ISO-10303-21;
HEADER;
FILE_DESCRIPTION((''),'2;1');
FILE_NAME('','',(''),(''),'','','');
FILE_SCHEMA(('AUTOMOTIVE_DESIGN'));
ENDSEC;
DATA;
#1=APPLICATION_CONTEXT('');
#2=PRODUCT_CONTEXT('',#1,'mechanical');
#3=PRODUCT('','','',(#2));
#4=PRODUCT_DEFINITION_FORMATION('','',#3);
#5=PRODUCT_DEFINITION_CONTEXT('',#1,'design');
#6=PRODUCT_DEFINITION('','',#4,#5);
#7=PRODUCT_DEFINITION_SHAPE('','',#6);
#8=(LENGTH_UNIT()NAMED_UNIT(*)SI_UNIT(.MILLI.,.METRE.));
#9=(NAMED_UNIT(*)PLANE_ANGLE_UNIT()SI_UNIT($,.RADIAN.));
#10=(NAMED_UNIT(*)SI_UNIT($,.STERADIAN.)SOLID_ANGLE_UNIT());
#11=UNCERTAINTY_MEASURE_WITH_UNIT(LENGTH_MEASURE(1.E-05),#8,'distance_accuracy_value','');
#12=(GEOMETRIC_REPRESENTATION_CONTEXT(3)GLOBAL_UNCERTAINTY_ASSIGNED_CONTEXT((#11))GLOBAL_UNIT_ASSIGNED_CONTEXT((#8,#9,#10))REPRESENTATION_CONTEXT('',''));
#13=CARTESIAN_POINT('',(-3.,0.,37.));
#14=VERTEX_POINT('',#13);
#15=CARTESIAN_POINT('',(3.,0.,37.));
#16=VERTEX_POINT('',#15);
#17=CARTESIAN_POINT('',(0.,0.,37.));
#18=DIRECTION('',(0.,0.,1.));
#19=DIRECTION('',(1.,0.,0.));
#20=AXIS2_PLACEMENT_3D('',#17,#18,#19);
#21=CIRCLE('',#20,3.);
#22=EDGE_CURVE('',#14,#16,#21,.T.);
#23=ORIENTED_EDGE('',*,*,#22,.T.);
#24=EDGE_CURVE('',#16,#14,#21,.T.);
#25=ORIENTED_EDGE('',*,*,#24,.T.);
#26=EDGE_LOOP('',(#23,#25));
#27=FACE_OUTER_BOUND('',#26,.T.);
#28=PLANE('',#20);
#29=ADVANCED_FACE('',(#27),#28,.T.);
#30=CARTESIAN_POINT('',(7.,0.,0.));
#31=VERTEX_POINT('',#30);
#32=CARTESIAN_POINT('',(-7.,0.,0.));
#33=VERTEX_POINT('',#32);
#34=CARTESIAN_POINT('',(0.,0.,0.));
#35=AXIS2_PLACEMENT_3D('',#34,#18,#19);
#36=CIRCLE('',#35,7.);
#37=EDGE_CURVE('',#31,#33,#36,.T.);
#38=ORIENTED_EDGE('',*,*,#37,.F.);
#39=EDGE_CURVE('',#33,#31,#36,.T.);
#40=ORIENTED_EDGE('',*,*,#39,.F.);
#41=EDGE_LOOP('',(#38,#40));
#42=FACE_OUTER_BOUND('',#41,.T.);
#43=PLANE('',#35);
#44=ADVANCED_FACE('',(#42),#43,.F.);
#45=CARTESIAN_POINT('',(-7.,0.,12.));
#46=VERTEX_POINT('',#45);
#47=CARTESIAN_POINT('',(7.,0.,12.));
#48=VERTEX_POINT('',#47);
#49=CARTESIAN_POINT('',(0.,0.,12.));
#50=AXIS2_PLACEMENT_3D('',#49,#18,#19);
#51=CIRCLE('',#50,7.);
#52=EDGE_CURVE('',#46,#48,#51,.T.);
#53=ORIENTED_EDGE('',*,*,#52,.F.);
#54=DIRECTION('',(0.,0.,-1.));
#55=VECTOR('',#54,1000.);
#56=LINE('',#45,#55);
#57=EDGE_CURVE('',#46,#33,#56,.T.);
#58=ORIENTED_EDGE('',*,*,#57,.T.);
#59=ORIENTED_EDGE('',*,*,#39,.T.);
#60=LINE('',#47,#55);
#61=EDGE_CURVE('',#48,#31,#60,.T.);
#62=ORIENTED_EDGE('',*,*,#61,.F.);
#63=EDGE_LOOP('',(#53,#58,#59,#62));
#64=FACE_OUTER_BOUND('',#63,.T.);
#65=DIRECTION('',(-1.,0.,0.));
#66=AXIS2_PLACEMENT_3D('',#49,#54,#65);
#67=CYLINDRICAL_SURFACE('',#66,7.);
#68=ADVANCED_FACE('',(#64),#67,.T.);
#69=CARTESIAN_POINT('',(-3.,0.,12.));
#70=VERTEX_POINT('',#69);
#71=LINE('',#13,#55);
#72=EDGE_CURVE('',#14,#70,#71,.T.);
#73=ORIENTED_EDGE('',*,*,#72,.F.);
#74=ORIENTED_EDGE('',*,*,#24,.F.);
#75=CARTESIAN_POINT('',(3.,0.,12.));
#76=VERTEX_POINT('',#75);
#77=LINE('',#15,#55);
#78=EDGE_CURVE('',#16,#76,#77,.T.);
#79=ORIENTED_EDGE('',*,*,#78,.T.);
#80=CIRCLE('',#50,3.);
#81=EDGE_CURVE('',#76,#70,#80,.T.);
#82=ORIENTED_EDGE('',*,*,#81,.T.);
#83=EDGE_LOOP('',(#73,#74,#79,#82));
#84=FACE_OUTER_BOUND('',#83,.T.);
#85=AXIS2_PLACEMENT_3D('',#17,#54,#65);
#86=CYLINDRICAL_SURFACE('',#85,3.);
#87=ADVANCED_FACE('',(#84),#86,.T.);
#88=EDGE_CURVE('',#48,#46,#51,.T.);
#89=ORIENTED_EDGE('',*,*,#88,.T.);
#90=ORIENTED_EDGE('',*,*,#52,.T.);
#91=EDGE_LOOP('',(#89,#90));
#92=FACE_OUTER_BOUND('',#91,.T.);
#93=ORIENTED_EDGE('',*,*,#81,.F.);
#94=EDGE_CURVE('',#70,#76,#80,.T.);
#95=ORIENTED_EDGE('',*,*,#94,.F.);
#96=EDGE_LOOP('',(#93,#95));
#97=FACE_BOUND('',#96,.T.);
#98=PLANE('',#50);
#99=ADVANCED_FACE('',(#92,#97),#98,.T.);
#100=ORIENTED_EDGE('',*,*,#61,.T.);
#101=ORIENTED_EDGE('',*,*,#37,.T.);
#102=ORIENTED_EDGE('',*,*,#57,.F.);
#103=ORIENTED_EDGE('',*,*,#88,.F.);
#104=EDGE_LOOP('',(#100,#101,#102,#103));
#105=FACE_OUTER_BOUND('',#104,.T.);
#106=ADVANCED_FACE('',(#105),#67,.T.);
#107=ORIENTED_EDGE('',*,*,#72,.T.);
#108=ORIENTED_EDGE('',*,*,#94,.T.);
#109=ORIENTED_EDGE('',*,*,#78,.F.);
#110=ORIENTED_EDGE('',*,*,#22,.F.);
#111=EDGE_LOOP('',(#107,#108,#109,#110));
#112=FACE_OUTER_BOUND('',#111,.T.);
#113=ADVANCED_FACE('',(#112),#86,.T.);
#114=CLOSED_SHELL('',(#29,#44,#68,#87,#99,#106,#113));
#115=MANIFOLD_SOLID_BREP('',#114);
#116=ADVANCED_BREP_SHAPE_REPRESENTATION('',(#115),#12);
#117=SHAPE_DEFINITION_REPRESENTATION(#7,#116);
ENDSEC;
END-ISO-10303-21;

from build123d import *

# Parameters (mm, degrees)
SKETCH_1_R      = 7
EXTRUDE_1_DEPTH = 12
SKETCH_2_R      = 3
EXTRUDE_2_DEPTH = 25


with BuildPart() as part:
    # 草图1 → 凸台-拉伸1 (new body)
    with BuildSketch(Plane.XY):
        Circle(SKETCH_1_R)
    extrude(amount=EXTRUDE_1_DEPTH)

    # 草图2 → 凸台-拉伸2 (add)
    with BuildSketch(Plane.XY.offset(12)):
        Circle(SKETCH_2_R)
    extrude(amount=EXTRUDE_2_DEPTH)


solid = part.part
